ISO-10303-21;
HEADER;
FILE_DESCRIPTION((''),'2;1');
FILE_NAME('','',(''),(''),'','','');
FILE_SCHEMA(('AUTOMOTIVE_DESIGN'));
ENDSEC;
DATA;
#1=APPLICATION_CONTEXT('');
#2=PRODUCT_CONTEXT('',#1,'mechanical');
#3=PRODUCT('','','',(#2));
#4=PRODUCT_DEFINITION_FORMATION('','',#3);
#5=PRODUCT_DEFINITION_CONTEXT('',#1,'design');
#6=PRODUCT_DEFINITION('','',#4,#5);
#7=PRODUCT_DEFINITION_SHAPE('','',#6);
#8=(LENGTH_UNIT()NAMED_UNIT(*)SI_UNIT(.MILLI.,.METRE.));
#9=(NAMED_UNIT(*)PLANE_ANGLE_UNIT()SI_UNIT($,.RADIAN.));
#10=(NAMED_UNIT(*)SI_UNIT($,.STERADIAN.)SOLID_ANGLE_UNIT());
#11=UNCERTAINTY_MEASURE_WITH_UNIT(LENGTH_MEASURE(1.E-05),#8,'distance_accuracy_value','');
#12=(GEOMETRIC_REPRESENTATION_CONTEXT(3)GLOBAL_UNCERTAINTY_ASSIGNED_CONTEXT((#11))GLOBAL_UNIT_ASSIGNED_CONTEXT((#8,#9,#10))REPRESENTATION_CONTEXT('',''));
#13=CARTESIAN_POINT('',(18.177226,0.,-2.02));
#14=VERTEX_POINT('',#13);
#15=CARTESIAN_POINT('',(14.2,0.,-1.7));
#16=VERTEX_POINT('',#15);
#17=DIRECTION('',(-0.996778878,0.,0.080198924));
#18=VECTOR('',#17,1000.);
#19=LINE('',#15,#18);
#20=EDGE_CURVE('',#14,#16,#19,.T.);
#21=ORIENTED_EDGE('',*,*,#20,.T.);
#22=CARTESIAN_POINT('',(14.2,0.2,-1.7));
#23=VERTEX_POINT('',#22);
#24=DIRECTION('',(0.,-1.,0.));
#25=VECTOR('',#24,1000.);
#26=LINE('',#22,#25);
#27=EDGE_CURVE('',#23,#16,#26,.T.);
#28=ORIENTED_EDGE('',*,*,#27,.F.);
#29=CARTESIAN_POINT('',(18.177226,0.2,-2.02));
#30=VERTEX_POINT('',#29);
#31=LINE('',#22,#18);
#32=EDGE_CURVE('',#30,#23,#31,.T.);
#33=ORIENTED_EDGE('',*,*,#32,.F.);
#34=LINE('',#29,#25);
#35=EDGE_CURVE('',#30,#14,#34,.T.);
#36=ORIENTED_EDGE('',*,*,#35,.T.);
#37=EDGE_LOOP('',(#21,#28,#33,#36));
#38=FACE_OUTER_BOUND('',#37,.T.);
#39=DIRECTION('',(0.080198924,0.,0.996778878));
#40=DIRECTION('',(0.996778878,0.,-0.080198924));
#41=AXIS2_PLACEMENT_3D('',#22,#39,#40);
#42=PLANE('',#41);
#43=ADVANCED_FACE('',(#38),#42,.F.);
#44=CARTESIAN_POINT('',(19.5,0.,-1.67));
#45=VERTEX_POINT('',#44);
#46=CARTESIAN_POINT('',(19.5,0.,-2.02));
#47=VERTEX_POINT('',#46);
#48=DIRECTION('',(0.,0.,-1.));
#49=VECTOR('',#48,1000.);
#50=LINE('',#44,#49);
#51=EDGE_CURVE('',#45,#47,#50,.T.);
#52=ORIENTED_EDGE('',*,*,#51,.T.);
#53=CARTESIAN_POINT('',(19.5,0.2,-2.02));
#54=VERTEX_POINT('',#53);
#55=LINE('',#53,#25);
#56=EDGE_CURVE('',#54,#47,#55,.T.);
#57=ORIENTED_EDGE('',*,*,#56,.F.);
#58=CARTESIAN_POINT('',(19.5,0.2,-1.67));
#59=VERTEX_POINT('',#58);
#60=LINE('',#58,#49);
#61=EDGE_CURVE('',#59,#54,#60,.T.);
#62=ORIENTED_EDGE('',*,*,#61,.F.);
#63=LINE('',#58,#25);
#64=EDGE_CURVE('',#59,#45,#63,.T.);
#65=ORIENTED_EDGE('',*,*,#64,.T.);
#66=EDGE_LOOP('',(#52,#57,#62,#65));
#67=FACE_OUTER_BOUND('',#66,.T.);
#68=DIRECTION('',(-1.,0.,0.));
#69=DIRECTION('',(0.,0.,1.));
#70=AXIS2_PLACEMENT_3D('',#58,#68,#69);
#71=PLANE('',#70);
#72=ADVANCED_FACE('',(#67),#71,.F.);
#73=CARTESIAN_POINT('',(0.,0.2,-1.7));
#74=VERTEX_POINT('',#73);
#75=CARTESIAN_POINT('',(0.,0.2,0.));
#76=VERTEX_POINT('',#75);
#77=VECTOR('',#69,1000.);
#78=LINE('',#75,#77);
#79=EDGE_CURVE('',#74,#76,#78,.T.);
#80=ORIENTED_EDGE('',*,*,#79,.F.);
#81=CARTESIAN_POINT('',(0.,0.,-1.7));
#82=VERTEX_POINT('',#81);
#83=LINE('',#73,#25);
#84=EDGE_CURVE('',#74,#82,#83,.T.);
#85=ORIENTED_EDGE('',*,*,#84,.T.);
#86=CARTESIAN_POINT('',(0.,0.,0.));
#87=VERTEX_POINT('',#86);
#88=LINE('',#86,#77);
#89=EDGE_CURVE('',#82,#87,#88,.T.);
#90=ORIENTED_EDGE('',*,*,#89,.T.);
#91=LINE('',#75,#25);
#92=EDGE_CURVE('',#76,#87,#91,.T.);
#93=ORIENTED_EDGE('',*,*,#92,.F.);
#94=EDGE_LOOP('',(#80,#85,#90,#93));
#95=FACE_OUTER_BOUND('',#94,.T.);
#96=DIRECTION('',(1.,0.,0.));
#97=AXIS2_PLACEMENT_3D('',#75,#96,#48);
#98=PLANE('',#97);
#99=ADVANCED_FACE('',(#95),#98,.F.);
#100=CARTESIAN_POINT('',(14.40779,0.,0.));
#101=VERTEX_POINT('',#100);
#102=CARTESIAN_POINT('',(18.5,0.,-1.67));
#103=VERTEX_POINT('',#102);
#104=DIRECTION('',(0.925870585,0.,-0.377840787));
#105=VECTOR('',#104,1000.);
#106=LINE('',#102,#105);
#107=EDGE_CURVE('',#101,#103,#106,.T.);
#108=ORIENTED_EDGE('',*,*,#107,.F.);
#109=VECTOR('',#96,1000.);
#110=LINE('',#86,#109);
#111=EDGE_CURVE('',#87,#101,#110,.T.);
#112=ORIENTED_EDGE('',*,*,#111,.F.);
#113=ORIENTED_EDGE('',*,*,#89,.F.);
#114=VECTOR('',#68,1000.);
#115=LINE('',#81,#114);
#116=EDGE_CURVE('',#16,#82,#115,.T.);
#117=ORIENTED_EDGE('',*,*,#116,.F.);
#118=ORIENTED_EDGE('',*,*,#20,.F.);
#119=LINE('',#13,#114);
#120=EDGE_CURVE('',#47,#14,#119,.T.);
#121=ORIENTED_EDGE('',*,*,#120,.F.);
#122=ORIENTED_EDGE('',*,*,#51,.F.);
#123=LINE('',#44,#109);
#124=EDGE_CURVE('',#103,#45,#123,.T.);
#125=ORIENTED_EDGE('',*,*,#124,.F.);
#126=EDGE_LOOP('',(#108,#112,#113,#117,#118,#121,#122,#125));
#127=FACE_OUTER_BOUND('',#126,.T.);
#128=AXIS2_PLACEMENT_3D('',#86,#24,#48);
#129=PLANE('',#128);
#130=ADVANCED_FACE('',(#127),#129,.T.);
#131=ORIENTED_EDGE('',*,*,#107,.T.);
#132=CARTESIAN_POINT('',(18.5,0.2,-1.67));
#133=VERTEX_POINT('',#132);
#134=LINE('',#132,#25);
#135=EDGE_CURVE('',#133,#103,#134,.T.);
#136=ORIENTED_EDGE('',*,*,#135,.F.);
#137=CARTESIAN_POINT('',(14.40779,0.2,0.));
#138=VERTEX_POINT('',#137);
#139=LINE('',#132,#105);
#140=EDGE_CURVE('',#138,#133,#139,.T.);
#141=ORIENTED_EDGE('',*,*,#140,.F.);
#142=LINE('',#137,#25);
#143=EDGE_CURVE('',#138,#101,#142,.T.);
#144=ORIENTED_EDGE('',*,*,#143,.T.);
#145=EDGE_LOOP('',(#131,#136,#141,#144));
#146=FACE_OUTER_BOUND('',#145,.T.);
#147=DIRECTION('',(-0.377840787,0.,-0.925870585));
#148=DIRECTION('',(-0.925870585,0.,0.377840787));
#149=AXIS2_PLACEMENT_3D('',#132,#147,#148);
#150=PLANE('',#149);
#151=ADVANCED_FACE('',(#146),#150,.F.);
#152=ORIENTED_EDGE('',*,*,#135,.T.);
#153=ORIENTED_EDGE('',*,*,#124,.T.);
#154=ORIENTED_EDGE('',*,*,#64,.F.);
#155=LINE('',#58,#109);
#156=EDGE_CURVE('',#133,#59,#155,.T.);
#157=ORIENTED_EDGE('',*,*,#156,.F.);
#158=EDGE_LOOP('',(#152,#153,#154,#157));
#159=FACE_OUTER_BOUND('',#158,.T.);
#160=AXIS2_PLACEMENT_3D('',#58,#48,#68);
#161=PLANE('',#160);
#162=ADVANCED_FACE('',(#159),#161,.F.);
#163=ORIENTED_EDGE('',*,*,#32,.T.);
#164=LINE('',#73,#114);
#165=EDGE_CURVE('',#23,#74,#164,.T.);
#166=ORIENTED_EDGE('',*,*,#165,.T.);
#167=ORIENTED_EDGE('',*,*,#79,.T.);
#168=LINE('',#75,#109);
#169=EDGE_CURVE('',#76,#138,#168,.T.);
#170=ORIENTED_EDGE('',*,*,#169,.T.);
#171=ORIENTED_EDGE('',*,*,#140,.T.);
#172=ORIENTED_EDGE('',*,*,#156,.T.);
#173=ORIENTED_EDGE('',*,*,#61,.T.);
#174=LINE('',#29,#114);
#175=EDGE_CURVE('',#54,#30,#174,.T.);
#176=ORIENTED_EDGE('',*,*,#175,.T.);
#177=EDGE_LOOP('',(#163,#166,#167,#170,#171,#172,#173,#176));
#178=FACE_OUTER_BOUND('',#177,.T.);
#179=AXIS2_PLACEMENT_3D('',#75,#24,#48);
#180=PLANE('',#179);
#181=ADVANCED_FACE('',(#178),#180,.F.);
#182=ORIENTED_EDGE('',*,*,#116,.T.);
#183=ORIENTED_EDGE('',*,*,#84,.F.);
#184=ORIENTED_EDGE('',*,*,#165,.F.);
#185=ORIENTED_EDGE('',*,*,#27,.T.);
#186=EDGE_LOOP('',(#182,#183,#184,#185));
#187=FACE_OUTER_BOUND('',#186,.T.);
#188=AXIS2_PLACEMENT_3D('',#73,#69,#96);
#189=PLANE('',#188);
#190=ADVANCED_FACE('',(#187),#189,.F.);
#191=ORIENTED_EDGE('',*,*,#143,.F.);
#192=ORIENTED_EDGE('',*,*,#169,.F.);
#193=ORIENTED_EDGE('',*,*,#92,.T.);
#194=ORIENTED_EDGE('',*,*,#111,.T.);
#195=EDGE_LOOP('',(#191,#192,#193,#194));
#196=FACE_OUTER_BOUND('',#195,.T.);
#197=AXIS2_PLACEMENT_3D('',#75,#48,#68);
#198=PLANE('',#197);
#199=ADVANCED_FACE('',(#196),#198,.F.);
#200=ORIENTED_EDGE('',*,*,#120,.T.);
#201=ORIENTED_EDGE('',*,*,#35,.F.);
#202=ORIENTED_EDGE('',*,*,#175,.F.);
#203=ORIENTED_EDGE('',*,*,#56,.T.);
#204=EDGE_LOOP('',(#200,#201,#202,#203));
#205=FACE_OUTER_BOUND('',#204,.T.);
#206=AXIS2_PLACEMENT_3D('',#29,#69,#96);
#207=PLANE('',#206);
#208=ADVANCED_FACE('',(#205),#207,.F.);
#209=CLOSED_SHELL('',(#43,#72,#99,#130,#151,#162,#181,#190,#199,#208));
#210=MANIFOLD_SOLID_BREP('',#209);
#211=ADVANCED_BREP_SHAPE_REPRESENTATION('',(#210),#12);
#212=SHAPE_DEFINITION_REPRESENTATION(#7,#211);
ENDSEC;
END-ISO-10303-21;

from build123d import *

# Parameters (mm, degrees)
BOSS_EXTRUDE1_DEPTH = 0.2


with BuildPart() as part:
    # Sketch1 → Boss-Extrude1 (new body)
    with BuildSketch(Plane(origin=(0, 0, 0), x_dir=(1, 0, 0), z_dir=(0, 1, 0))):
        Polygon((19.5, 1.67), (18.5, 1.67), (14.40778992, 0), (0, 0), (0, 1.7), (14.2, 1.7), (18.177225926, 2.02), (19.5, 2.02), align=None)
    extrude(amount=BOSS_EXTRUDE1_DEPTH)


solid = part.part
